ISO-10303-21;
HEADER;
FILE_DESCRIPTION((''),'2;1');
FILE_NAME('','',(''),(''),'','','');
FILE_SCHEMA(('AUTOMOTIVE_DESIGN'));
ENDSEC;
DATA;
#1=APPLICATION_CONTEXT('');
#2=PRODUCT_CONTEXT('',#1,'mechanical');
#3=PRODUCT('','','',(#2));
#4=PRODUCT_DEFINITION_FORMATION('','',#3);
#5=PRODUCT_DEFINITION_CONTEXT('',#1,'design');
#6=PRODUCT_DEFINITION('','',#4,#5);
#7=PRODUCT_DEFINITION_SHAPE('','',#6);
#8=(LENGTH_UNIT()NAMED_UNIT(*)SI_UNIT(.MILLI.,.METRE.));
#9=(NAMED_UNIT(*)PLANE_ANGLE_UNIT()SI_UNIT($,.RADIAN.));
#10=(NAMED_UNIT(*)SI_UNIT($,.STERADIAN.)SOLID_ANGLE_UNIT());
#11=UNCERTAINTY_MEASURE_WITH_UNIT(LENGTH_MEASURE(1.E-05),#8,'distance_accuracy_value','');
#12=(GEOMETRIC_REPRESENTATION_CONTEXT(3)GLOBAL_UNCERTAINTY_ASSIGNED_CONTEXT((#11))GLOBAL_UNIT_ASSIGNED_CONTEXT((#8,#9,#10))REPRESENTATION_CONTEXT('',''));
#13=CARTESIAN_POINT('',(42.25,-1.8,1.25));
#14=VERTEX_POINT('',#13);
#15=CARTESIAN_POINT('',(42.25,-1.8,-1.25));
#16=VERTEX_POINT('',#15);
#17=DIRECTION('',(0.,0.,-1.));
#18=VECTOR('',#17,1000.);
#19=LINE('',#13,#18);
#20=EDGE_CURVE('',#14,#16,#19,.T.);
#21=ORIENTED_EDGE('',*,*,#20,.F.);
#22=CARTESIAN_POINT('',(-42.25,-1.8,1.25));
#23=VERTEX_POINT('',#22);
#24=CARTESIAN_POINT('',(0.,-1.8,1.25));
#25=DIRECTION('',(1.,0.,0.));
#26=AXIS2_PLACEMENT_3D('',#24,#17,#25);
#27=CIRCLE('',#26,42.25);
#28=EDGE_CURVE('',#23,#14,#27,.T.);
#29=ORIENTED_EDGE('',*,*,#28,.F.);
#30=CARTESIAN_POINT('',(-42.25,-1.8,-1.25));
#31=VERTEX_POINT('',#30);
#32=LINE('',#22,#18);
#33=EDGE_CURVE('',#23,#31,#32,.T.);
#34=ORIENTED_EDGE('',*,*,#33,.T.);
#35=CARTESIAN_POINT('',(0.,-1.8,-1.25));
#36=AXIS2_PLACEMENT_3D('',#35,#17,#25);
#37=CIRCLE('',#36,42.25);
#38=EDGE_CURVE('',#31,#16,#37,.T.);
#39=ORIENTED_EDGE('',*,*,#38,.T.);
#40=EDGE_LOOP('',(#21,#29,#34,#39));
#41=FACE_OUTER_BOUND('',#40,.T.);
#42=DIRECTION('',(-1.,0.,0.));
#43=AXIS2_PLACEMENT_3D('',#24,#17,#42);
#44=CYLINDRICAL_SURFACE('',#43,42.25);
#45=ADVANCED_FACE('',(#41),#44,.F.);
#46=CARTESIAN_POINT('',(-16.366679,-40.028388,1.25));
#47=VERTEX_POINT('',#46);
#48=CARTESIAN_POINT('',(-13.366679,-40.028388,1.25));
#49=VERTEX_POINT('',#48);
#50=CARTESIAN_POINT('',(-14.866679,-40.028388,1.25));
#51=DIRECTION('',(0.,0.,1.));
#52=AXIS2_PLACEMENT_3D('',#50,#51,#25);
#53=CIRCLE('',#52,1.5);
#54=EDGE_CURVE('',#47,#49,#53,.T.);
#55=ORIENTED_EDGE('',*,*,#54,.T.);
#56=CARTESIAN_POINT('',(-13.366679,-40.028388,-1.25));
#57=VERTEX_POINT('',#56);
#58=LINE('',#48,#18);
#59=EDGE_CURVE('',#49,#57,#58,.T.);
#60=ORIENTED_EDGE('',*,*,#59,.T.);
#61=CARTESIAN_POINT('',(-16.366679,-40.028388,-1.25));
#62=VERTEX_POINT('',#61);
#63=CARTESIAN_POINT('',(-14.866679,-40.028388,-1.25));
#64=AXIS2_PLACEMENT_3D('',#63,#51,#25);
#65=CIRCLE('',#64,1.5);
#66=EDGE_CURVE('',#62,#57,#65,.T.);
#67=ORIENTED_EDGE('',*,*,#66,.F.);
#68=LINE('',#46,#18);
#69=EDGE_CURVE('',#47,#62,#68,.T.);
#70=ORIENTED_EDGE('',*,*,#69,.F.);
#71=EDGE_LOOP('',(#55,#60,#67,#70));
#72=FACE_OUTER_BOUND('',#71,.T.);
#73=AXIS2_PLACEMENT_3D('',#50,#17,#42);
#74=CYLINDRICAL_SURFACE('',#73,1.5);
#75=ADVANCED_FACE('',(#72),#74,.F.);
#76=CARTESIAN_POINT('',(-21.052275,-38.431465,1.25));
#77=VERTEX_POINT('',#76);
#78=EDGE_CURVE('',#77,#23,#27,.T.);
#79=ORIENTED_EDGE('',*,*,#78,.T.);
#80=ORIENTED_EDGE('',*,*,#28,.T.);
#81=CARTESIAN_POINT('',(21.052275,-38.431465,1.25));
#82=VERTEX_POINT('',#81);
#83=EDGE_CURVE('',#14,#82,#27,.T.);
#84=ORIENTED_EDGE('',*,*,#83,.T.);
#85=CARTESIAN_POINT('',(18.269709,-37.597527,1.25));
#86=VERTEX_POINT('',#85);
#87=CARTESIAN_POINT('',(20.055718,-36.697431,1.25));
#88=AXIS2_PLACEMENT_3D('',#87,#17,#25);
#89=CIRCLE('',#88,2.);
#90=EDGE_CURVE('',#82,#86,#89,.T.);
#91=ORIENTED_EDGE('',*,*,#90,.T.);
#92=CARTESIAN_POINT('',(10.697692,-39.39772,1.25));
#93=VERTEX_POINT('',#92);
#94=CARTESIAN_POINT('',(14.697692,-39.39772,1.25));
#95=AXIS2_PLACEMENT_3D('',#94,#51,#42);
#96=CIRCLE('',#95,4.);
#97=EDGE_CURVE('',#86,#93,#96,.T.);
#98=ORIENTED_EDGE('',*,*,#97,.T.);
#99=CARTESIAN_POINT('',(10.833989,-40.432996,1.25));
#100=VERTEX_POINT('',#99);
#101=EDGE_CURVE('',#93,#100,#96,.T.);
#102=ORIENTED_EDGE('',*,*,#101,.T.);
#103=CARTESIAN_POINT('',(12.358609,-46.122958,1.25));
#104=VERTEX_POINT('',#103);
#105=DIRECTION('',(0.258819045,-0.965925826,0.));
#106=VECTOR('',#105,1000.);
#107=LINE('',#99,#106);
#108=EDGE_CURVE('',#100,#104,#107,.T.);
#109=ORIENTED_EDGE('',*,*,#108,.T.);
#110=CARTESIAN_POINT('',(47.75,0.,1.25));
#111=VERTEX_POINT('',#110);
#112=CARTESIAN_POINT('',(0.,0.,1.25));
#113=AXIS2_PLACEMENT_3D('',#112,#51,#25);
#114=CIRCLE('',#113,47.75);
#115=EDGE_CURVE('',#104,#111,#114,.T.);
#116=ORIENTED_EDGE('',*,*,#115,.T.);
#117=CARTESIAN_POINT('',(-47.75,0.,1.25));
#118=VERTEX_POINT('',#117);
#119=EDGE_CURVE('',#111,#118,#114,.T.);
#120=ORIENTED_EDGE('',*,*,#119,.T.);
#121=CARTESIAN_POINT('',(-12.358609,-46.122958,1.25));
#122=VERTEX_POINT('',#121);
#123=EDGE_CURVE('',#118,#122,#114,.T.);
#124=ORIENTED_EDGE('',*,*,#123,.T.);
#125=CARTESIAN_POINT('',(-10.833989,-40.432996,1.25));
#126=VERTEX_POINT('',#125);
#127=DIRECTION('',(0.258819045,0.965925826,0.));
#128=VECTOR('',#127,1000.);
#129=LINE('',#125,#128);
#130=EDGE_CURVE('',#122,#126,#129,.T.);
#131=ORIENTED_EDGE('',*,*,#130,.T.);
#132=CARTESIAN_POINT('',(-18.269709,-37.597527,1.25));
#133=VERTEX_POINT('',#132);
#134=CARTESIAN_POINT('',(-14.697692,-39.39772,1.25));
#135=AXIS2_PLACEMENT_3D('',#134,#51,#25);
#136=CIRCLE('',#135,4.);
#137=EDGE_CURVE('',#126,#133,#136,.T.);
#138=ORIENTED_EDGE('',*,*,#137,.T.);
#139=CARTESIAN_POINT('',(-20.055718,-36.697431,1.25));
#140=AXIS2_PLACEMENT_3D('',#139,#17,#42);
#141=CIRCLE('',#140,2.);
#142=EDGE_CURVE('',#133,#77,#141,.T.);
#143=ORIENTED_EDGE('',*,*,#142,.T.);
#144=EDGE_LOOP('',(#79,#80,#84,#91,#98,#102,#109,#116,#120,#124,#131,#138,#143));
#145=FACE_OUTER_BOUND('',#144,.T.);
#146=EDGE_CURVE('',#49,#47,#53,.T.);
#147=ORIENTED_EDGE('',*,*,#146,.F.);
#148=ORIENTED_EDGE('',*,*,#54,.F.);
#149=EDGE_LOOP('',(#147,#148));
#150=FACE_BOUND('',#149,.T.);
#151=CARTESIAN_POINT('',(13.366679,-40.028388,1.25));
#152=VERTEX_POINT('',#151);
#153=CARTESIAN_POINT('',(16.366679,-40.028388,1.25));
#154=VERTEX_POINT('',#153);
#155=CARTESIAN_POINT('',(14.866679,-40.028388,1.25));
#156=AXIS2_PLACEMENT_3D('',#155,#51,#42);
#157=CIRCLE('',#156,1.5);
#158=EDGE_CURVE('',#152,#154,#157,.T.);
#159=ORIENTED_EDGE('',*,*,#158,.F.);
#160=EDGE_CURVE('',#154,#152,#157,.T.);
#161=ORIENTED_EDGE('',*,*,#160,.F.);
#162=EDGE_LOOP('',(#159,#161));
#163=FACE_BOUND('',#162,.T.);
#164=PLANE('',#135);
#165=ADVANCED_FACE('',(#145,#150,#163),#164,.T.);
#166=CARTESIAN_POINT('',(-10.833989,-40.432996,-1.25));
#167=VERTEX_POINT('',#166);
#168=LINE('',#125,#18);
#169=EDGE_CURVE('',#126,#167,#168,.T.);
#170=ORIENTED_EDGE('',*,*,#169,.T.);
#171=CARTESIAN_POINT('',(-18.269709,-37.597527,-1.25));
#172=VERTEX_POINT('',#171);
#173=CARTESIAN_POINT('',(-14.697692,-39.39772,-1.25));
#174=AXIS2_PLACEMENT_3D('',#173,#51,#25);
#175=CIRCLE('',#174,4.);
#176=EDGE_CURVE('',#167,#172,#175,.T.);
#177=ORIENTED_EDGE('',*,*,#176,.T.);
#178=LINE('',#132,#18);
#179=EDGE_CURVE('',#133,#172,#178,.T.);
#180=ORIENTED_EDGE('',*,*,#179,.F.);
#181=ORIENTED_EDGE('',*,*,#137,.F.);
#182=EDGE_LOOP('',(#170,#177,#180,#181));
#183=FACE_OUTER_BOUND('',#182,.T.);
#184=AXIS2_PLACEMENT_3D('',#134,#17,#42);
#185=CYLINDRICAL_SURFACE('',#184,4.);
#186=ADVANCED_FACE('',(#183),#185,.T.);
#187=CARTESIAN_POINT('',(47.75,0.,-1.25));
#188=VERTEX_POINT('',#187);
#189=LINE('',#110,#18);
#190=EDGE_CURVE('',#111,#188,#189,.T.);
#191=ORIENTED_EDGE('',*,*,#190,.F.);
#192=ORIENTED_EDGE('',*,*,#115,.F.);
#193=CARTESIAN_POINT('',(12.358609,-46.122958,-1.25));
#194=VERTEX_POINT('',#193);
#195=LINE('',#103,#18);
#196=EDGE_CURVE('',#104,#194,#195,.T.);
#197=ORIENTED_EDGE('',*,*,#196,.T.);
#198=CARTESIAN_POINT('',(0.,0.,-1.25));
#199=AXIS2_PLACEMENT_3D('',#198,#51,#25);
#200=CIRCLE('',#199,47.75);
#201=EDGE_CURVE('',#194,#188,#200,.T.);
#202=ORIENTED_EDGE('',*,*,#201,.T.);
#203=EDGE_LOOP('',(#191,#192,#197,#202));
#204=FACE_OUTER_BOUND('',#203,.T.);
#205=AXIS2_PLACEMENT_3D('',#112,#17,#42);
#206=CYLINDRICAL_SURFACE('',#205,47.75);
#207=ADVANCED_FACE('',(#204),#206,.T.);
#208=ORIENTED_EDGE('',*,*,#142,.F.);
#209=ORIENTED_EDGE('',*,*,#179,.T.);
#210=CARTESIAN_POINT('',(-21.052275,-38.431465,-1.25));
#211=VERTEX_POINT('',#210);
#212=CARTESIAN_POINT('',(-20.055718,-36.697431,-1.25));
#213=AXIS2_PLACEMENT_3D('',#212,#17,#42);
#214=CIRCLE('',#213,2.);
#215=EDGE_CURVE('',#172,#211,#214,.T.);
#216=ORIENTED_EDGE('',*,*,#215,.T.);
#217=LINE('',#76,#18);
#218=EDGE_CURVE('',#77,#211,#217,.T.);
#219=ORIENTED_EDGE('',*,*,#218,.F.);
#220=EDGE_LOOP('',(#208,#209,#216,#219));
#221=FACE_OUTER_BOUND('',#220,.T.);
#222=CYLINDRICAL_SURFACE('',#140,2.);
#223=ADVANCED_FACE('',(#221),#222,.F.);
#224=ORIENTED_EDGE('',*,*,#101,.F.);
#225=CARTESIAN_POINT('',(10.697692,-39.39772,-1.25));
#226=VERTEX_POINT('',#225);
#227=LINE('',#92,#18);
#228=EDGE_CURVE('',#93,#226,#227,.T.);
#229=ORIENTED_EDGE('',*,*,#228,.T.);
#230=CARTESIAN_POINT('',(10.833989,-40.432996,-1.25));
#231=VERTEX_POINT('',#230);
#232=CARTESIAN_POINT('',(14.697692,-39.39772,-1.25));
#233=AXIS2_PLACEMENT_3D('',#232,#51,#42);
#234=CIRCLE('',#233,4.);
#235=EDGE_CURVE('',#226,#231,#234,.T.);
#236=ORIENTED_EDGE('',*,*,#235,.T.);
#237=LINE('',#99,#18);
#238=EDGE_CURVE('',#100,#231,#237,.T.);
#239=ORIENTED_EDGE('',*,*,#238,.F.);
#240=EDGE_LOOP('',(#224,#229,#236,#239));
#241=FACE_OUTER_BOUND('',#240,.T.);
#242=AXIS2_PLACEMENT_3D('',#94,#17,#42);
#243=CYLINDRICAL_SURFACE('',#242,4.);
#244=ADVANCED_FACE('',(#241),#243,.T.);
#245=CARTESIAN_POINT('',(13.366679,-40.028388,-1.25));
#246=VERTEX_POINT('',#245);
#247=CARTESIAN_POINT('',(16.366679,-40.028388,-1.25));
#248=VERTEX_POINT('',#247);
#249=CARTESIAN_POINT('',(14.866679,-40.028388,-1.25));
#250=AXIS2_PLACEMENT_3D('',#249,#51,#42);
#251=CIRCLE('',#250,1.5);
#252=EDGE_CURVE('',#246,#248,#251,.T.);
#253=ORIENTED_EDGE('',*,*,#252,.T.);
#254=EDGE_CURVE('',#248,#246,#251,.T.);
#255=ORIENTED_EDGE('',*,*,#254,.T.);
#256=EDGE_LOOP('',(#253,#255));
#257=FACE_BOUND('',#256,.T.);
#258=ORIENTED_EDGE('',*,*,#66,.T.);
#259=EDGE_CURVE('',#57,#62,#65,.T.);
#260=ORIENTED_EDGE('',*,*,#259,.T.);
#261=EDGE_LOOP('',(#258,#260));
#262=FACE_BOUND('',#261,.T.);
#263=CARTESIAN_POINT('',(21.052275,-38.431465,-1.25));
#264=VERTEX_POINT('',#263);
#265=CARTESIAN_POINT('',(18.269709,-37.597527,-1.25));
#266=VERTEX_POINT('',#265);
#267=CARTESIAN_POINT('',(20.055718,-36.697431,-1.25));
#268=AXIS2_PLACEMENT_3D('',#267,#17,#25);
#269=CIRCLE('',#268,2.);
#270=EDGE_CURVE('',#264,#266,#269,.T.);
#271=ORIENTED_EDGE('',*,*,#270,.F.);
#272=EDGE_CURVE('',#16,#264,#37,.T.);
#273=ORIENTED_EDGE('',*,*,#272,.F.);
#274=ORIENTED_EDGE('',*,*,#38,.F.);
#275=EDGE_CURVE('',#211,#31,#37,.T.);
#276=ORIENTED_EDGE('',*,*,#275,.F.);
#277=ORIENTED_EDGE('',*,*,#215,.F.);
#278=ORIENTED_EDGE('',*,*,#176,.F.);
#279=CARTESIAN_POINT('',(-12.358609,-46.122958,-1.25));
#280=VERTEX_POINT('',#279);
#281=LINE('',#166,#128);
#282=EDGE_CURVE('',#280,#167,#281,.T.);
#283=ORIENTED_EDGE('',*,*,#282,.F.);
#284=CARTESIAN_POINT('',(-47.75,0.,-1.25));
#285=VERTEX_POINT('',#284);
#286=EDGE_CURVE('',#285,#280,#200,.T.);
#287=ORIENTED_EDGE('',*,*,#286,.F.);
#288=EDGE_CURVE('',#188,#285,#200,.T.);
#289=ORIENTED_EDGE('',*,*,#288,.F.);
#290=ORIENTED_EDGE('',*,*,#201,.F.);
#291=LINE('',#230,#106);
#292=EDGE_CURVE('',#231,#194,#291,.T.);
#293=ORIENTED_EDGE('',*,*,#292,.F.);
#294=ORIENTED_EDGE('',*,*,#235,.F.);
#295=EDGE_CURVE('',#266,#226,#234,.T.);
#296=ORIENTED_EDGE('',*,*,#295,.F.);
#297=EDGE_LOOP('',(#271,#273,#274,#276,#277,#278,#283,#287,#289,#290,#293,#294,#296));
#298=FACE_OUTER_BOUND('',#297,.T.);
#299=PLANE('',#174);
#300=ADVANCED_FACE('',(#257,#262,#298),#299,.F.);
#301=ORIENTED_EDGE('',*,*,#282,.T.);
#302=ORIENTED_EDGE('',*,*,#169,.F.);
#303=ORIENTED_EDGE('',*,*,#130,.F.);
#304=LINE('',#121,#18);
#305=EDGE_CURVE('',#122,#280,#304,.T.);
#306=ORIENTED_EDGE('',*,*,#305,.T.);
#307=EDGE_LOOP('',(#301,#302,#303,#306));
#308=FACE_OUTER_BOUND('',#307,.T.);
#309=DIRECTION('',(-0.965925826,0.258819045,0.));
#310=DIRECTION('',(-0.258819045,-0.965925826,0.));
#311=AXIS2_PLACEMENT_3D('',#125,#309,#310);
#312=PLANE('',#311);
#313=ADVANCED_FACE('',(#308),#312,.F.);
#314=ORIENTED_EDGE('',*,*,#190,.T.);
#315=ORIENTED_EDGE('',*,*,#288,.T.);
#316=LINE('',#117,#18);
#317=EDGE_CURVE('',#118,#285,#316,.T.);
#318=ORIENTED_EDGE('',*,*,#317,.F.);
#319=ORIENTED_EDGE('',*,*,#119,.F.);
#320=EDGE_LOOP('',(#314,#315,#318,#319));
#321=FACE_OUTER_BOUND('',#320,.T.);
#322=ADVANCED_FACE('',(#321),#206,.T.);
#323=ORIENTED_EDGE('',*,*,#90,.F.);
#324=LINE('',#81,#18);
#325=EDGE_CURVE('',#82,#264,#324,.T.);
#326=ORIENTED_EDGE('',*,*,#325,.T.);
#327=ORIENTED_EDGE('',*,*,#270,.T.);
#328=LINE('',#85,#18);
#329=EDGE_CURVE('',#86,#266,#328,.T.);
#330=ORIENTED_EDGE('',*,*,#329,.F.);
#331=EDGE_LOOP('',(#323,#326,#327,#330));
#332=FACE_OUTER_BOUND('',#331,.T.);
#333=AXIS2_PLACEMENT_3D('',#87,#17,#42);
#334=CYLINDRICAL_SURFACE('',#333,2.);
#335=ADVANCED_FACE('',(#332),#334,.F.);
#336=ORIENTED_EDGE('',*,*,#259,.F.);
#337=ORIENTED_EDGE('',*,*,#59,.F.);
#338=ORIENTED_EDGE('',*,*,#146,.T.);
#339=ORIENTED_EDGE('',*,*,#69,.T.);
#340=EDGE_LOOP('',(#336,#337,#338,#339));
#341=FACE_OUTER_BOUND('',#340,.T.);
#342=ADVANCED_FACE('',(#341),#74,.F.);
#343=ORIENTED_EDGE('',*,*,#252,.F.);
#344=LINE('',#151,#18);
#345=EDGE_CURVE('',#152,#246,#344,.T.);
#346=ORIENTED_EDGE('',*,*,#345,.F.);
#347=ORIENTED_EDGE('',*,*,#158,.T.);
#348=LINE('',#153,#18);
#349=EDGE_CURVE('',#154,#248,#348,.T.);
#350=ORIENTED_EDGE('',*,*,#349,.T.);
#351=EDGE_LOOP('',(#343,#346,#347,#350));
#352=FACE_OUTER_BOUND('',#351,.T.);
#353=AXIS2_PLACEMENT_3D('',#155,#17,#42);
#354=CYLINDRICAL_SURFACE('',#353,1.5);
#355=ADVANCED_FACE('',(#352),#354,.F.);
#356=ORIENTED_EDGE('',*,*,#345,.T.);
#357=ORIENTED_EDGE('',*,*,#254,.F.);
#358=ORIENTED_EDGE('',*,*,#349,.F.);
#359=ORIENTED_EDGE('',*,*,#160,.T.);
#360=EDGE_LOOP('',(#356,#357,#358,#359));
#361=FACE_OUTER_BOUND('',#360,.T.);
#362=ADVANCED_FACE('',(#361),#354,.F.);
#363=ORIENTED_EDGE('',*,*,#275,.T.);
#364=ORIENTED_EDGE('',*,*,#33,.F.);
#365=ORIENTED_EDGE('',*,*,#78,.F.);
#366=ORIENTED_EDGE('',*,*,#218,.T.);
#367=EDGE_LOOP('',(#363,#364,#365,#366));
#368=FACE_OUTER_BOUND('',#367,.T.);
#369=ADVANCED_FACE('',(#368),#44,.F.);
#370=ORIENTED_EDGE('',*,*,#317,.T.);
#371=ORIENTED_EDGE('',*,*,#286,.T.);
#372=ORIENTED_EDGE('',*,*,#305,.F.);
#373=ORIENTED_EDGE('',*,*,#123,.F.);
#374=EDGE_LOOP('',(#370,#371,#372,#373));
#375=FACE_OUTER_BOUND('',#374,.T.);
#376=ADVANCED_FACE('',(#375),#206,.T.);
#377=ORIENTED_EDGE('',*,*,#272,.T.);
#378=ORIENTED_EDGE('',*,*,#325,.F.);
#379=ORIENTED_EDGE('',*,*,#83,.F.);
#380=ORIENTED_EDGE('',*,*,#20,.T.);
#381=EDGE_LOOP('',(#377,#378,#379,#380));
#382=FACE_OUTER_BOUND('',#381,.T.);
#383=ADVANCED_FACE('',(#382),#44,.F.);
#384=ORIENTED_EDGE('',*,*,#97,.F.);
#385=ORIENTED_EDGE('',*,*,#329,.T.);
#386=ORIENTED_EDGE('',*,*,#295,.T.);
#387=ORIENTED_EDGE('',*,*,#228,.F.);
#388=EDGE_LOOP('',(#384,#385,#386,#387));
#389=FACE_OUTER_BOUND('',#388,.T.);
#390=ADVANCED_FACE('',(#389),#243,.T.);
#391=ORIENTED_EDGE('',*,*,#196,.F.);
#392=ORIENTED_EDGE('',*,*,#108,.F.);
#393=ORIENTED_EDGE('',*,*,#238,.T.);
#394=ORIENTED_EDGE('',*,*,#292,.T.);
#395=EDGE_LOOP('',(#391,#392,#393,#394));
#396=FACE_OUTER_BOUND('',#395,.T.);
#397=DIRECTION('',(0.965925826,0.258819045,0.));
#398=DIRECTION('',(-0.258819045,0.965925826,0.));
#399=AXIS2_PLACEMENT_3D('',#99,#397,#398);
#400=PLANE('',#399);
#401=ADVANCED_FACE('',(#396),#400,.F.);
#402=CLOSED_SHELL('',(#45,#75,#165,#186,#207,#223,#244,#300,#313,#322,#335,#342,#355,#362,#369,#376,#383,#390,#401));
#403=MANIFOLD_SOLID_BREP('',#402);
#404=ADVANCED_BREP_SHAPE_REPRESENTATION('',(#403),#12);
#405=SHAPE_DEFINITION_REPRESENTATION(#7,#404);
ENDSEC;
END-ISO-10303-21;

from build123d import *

# Parameters (mm, degrees)
EXTRUDE_962_DEPTH      = 1.25
EXTRUDE_962_DEPTH_BACK = 1.25
SKETCH_1_R             = 1.5


with BuildPart() as part:
    # 草图1 → Extrude 962 (new, two sides: drawn at the far end of the back side and taken through both)
    with BuildSketch(Plane.XY.offset(-EXTRUDE_962_DEPTH_BACK)):
        with BuildLine():
            Line((-10.833988703, -40.432996288), (-12.358609404, -46.122958205))
            ThreePointArc((-12.358609404, -46.122958205), (0, 47.75), (12.358609404, -46.122958205))
            Line((12.358609404, -46.122958205), (10.833988703, -40.432996288))
            ThreePointArc((10.833988703, -40.432996288), (13.272475808, -35.660239835), (18.269709097, -37.597527364))
            ThreePointArc((18.269709097, -37.597527364), (19.48154763, -38.613241212), (21.05227504, -38.43146483))
            ThreePointArc((21.05227504, -38.43146483), (0, 40.45), (-21.05227504, -38.43146483))
            ThreePointArc((-21.05227504, -38.43146483), (-19.48154763, -38.613241212), (-18.269709097, -37.597527364))
            ThreePointArc((-18.269709097, -37.597527364), (-13.272475808, -35.660239835), (-10.833988703, -40.432996288))
        make_face()
        with Locations((-14.866678993, -40.028388123)):
            Circle(SKETCH_1_R, mode=Mode.SUBTRACT)
        with Locations(Location((14.866678993, -40.028388123, 0), (0, 0, 180))):
            Circle(SKETCH_1_R, mode=Mode.SUBTRACT)
    extrude(amount=EXTRUDE_962_DEPTH + EXTRUDE_962_DEPTH_BACK)


solid = part.part
